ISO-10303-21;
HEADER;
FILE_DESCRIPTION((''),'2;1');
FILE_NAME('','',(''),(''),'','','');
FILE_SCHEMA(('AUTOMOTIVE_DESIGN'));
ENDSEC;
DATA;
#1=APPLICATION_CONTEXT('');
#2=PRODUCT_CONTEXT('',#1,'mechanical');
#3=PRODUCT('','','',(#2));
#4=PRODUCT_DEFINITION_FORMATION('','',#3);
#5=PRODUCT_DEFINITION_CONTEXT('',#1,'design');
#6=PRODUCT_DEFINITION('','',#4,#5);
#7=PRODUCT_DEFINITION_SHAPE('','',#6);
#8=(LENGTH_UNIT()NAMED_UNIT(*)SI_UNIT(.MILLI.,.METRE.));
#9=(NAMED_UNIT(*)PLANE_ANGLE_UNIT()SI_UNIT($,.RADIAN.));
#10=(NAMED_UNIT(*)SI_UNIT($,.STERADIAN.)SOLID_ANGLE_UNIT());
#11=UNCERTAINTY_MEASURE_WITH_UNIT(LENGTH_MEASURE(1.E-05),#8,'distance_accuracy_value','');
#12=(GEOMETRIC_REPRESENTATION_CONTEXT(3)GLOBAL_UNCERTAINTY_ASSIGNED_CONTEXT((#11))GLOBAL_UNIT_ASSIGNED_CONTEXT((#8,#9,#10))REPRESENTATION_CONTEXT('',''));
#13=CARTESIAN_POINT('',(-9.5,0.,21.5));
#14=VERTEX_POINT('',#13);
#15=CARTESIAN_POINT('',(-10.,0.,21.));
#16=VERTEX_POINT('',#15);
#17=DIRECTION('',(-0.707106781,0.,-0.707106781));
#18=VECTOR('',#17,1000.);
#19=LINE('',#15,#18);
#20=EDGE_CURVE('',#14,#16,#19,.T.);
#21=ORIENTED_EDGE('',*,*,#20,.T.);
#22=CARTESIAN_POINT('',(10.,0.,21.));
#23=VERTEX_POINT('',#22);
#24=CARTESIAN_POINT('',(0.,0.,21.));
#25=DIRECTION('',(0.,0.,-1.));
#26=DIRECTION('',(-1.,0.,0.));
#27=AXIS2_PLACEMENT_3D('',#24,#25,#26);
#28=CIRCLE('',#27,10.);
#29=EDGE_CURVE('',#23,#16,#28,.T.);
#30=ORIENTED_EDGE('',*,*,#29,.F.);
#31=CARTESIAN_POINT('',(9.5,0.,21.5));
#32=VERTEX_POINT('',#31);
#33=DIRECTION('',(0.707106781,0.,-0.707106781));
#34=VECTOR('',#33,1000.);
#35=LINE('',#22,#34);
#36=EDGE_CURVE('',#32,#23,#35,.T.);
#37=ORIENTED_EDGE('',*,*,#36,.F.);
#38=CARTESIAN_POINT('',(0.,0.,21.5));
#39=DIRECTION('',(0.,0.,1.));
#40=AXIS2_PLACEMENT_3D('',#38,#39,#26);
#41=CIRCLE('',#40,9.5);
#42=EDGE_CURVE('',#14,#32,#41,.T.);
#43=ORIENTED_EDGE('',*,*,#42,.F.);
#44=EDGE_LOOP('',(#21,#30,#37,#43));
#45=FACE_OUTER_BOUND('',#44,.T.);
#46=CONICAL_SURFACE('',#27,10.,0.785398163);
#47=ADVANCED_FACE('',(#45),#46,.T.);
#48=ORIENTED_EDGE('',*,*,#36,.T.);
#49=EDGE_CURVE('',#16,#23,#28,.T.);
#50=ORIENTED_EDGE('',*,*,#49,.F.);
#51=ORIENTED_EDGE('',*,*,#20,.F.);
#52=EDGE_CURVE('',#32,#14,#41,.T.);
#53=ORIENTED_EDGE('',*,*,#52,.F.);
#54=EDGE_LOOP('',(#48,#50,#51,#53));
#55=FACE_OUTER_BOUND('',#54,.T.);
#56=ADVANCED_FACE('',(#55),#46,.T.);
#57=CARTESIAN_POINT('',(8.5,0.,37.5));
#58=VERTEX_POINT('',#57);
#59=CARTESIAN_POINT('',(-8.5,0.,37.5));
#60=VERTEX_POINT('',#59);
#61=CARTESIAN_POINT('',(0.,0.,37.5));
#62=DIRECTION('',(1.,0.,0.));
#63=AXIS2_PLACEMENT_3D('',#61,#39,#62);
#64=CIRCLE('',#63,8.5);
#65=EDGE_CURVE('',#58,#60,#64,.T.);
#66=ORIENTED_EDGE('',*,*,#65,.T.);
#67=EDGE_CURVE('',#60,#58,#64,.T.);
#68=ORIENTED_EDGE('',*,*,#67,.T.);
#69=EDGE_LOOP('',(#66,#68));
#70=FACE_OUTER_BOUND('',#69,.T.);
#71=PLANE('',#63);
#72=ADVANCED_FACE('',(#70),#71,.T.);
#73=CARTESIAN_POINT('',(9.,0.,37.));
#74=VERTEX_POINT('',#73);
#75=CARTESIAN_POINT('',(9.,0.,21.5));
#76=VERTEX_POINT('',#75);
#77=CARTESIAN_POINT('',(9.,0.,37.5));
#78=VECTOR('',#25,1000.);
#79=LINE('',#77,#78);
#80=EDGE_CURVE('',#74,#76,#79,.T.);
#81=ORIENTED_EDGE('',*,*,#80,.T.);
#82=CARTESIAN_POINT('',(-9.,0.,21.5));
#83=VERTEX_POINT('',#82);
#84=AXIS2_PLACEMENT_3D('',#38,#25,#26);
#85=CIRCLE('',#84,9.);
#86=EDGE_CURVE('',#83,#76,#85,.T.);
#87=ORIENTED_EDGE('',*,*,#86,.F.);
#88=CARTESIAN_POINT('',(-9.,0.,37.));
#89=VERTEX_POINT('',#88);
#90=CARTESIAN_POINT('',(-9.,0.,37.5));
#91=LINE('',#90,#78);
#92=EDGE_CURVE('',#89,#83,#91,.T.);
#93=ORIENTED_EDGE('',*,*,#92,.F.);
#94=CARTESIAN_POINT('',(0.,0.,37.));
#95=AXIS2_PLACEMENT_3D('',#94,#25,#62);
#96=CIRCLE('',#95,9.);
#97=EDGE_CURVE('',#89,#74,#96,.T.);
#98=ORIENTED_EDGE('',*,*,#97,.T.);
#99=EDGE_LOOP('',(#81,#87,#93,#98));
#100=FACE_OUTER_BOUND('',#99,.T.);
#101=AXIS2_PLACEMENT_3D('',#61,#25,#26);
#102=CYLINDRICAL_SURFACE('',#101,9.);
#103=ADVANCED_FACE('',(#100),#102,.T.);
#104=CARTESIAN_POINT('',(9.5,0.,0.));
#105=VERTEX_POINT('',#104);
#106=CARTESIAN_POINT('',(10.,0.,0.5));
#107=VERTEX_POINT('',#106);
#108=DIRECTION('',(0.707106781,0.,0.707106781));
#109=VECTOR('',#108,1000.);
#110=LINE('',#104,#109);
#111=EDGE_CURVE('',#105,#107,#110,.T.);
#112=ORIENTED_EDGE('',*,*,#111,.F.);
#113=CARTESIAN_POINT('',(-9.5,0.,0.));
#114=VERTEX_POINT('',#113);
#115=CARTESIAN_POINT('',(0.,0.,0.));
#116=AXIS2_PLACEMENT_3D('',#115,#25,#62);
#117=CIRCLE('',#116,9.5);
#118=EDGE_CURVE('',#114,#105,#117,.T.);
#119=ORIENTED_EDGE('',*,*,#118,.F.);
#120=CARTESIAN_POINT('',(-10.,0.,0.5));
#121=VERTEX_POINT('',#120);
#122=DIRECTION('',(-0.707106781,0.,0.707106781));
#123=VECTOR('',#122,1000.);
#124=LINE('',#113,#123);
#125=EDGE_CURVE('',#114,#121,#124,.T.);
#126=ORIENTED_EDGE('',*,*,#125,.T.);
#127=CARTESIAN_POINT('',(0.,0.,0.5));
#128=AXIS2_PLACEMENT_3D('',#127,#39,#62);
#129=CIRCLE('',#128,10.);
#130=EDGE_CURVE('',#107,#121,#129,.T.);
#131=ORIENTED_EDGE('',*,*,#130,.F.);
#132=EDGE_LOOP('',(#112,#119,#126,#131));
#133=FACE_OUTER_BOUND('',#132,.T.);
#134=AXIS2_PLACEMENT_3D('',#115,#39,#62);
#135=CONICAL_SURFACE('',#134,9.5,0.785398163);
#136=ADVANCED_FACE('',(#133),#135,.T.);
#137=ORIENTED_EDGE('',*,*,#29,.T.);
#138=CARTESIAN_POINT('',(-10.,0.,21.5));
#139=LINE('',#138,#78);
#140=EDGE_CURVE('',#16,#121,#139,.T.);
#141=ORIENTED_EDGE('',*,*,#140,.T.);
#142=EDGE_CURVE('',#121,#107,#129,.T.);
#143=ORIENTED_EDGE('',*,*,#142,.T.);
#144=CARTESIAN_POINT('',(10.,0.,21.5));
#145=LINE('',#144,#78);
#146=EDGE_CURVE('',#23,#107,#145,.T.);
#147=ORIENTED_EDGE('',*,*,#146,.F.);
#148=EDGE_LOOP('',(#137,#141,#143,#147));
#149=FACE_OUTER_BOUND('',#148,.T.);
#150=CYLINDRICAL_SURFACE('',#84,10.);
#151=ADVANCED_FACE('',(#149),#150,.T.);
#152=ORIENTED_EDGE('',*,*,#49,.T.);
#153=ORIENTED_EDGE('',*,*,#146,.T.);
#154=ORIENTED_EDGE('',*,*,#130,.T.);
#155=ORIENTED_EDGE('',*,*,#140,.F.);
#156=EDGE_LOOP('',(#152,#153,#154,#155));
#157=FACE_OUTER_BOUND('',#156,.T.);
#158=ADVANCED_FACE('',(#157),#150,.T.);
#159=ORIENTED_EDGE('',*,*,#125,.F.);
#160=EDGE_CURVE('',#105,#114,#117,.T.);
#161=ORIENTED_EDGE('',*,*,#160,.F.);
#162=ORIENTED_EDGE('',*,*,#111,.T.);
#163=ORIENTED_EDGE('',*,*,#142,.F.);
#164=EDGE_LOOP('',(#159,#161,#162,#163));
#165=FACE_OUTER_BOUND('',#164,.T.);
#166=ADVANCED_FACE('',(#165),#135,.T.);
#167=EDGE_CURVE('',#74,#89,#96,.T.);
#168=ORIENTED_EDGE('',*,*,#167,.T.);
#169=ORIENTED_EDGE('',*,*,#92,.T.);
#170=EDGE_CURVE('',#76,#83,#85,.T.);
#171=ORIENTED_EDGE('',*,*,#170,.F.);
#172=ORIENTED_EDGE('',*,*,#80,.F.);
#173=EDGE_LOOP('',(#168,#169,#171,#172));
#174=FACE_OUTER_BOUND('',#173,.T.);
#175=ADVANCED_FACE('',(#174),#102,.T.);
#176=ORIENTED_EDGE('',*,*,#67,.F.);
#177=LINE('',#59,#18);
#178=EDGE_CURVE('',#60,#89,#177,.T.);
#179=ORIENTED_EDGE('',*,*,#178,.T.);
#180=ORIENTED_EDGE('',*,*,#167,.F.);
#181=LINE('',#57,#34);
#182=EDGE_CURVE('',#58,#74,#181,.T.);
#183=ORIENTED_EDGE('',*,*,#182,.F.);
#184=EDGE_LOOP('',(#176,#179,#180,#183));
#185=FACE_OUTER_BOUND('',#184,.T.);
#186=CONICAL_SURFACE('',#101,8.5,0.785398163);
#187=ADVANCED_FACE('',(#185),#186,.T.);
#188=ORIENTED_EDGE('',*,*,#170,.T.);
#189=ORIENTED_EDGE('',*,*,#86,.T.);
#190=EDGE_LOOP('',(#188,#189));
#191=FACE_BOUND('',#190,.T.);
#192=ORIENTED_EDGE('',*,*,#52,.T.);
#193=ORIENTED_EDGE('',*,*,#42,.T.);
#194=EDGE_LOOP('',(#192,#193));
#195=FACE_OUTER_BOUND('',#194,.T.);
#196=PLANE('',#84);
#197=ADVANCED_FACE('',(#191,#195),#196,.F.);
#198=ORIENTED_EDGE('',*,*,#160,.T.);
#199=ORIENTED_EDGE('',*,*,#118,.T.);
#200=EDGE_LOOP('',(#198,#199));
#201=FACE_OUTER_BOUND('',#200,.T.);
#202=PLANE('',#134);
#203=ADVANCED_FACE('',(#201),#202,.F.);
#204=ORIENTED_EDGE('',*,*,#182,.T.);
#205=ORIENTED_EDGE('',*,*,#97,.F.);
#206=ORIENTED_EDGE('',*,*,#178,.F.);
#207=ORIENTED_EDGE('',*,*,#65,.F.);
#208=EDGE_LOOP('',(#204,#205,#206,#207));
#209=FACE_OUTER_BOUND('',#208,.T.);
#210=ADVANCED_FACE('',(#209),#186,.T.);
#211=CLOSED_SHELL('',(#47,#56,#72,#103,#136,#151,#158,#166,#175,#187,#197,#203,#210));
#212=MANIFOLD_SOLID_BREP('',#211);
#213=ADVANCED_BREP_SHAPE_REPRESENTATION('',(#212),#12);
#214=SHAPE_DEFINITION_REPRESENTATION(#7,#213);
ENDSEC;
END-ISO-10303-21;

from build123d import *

# Parameters (mm, degrees)
SKETCH1_R           = 9
BOSS_EXTRUDE1_DEPTH = 37.5
SKETCH2_R           = 10
BOSS_EXTRUDE2_DEPTH = 21.5
CHAMFER1_SIZE       = 0.5


with BuildPart() as part:
    # Sketch1 → Boss-Extrude1 (new body)
    with BuildSketch(Plane.XY):
        Circle(SKETCH1_R)
    extrude(amount=BOSS_EXTRUDE1_DEPTH)

    # Sketch2 → Boss-Extrude2 (add)
    with BuildSketch(Plane(origin=(0, 0, 0), x_dir=(-1, 0, 0), z_dir=(0, 0, -1))):
        Circle(SKETCH2_R)
    extrude(amount=-BOSS_EXTRUDE2_DEPTH)

    # Chamfer1
    chamfer1_edges = [part.edges().sort_by_distance(p)[0] for p in [
        (-9, 0, 37.5),
        (10, 0, 21.5),
        (10, 0, 0),
    ]]
    chamfer(chamfer1_edges, length=CHAMFER1_SIZE)


solid = part.part
